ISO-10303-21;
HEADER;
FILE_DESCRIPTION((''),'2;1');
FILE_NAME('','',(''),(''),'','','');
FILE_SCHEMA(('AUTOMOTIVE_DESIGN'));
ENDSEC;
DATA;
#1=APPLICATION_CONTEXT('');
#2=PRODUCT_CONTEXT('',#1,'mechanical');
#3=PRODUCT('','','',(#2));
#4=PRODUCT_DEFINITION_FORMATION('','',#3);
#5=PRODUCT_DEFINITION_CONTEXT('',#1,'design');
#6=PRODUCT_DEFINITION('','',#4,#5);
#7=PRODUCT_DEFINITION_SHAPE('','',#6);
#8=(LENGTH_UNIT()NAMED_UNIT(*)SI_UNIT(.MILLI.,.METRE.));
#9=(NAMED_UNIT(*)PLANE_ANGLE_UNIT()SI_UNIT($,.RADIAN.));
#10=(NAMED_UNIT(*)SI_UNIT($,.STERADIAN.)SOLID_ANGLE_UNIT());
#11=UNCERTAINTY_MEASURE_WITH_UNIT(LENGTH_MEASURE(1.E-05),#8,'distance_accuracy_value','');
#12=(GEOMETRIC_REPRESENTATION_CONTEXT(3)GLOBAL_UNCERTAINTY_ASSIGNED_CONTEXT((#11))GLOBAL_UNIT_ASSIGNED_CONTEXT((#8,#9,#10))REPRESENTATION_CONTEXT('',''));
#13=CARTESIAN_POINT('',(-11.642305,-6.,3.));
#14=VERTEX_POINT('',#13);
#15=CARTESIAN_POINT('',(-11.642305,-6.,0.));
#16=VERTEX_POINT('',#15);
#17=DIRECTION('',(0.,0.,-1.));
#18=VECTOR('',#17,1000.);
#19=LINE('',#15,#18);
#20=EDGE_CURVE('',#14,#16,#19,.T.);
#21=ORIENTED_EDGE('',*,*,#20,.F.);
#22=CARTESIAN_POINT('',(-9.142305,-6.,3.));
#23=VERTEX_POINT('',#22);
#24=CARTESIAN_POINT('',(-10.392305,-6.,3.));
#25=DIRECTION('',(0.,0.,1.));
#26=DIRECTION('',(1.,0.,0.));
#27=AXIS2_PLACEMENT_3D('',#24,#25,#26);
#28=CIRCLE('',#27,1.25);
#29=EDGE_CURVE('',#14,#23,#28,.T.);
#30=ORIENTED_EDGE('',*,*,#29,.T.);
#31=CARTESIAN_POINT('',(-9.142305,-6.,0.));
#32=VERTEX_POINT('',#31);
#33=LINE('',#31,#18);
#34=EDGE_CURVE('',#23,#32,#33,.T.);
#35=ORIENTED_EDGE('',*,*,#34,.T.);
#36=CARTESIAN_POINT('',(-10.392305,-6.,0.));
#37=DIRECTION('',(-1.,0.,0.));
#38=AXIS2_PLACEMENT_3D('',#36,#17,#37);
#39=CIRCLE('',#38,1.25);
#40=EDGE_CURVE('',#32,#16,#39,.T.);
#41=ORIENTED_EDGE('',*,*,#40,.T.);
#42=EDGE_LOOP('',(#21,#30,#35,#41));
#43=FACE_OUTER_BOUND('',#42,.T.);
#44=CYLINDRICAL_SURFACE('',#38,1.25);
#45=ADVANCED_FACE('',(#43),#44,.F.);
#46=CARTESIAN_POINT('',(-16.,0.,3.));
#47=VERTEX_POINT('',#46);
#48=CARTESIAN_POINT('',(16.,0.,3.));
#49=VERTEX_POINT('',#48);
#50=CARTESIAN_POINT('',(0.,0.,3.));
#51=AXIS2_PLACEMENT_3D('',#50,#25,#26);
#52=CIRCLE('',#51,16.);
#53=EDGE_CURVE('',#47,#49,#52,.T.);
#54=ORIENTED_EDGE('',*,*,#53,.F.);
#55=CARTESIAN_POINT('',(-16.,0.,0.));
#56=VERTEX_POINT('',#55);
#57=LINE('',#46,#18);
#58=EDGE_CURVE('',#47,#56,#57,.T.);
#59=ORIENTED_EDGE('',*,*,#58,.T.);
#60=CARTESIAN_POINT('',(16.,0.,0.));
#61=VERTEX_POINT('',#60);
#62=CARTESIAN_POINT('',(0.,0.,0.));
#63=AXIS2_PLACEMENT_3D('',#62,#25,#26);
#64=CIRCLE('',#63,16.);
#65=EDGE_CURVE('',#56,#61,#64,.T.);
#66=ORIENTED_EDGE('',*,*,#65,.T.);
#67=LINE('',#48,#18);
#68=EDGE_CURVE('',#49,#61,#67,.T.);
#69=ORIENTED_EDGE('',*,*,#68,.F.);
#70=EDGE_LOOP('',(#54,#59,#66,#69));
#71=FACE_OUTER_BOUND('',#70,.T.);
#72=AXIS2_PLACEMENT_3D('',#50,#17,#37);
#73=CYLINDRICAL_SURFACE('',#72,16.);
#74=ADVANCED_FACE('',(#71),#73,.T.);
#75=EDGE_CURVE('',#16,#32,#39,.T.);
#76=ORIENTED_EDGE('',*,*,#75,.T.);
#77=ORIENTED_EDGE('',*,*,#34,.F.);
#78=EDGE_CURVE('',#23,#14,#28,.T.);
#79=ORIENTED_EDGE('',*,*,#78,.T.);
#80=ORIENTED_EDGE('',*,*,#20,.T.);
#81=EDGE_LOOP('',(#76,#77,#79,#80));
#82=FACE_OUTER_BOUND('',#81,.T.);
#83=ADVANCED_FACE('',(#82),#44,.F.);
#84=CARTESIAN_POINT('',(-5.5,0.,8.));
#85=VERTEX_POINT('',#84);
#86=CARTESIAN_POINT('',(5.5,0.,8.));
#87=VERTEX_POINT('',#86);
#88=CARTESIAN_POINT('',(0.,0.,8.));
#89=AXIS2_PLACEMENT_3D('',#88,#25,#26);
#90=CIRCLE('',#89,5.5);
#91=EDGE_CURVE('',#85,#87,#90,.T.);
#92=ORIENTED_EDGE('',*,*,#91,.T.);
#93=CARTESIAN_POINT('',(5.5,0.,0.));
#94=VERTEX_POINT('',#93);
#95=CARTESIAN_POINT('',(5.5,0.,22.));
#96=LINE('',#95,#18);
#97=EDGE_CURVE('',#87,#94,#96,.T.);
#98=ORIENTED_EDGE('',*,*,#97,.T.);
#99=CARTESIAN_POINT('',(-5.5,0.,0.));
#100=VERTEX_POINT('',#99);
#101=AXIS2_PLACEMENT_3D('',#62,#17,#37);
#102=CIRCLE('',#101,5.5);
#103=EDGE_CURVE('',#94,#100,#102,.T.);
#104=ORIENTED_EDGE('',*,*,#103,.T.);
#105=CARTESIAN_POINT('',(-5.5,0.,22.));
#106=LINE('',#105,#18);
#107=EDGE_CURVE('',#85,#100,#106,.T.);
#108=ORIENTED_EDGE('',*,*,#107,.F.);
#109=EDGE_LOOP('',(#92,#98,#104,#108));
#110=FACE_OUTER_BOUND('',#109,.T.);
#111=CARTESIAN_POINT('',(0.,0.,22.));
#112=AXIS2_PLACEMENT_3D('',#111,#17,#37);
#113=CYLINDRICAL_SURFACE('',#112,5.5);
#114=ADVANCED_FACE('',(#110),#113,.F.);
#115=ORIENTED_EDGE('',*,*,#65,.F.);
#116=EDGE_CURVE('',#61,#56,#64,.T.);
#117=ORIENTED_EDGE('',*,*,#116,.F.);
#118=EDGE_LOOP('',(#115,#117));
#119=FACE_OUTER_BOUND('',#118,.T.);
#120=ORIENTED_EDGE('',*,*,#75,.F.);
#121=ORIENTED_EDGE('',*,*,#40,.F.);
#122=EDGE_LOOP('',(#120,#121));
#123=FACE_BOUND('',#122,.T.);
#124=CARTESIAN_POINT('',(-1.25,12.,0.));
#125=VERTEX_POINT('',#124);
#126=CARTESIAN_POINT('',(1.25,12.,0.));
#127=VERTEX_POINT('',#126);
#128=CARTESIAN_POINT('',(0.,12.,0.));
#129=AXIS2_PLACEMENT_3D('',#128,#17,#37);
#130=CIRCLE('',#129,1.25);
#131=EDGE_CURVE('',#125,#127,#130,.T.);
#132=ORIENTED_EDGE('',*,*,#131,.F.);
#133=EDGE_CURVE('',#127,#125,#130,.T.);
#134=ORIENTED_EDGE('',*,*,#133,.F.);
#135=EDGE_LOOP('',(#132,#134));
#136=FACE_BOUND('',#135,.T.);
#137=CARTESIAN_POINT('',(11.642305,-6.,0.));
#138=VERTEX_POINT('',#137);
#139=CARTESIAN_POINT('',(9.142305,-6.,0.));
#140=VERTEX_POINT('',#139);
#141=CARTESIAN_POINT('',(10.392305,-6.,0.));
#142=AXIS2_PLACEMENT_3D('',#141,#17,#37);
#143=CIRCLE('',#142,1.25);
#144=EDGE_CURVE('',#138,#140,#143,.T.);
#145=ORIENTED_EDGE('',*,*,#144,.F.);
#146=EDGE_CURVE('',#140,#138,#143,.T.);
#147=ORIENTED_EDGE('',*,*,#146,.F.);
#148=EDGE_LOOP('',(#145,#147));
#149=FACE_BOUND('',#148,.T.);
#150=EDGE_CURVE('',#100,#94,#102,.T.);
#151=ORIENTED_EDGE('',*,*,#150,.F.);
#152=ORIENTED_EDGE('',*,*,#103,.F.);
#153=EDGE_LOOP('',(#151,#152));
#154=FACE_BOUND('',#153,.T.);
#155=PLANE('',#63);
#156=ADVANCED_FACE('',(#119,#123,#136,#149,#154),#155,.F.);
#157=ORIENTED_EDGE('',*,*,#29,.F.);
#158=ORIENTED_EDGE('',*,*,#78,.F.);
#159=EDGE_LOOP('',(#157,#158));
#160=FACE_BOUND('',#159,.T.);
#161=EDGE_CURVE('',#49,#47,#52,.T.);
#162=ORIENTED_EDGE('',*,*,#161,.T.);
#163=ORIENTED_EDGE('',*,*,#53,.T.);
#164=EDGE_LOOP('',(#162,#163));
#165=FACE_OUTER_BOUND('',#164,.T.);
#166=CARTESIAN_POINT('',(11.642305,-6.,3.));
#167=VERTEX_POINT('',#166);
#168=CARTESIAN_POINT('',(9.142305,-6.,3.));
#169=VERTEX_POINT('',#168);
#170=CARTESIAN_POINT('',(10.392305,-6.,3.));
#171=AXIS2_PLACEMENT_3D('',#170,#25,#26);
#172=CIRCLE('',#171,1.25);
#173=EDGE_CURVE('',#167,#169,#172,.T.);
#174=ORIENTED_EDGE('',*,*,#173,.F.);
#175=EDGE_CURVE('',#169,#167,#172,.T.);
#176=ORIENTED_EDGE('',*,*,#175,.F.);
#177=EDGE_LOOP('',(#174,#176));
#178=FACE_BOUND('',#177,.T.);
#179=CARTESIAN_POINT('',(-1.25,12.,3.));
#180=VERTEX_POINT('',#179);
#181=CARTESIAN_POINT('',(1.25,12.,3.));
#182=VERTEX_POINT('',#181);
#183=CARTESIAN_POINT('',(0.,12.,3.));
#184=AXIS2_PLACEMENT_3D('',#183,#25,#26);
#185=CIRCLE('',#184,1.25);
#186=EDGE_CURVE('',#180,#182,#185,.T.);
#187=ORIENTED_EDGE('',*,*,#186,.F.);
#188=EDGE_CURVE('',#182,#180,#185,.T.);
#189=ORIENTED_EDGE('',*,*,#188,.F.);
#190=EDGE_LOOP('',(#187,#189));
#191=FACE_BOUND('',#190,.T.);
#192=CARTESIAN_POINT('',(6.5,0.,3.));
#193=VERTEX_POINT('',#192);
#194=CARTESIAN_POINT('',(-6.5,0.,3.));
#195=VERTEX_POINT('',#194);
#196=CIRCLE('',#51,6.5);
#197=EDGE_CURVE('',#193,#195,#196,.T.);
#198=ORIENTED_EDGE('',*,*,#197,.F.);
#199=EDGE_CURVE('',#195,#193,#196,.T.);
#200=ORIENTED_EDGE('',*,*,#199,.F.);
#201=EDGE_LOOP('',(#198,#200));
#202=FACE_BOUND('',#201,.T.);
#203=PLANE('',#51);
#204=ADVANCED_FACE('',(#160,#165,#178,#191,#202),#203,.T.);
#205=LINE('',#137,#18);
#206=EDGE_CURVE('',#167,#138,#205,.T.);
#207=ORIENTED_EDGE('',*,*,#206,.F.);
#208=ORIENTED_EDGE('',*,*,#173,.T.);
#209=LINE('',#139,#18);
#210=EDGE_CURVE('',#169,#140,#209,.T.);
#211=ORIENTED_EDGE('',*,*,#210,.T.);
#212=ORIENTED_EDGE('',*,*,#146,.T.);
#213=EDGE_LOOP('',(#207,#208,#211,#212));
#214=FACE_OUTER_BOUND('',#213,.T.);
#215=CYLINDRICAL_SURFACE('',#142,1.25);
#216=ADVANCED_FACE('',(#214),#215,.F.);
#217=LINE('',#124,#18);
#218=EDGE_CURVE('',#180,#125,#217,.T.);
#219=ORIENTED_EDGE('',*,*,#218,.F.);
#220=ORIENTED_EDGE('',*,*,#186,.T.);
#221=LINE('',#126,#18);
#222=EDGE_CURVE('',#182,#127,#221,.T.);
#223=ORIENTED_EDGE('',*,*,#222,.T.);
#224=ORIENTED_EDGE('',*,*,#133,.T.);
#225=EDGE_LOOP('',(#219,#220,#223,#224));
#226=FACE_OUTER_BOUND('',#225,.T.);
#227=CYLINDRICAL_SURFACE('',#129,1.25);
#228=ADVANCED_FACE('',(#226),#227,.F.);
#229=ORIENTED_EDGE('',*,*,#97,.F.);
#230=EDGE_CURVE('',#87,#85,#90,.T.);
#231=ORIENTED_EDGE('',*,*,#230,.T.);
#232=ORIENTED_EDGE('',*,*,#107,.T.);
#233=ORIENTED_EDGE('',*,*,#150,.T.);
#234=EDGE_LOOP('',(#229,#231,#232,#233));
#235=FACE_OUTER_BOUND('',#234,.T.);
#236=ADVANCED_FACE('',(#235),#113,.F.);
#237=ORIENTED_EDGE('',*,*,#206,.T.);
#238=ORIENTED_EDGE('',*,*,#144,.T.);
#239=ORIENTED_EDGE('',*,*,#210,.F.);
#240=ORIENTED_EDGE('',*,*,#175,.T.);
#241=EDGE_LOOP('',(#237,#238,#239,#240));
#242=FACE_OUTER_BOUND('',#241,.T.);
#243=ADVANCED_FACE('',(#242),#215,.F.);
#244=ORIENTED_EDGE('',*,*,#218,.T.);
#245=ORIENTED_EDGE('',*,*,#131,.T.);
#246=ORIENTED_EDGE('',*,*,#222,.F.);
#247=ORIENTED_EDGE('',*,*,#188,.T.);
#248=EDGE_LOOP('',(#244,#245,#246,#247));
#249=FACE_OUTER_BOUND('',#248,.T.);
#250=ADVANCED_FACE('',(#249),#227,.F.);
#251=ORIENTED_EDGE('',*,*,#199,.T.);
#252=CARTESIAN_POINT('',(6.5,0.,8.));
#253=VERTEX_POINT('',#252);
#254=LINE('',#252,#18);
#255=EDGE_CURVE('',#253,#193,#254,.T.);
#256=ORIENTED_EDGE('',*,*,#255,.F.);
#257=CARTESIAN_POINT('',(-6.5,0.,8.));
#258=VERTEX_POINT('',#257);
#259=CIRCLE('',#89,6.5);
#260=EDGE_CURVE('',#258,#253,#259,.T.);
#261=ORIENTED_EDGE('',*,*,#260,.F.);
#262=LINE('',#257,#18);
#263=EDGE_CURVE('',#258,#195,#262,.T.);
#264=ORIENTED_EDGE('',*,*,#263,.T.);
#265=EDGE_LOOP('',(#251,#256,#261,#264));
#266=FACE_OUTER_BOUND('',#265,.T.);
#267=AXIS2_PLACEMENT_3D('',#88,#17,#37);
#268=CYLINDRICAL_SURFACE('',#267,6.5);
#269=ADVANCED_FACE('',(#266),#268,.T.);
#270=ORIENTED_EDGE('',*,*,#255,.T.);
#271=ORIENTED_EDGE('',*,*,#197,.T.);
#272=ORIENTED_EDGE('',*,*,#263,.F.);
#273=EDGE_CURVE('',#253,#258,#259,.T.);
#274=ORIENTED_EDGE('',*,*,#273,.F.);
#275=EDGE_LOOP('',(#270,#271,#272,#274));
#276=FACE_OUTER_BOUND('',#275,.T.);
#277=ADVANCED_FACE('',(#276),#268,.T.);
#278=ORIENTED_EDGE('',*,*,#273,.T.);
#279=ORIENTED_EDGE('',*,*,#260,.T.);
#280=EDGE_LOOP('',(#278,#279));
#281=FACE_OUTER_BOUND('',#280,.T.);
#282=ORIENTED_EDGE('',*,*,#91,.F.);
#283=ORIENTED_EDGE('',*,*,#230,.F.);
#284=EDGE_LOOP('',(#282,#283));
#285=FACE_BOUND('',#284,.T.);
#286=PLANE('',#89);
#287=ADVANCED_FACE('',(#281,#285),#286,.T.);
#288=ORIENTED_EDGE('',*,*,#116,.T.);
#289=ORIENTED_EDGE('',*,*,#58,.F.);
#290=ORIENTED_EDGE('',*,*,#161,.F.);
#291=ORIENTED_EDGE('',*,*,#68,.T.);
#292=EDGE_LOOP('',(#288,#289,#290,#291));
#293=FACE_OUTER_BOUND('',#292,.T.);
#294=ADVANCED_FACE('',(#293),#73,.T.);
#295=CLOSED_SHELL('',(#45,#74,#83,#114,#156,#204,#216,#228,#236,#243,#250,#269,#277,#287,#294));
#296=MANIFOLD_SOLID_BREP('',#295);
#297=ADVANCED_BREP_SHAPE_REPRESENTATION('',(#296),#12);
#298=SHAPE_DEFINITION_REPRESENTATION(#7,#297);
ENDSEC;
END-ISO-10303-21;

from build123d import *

# Parameters (mm, degrees)
SKETCH1_R             = 16
BOSS_EXTRUDE1_DEPTH   = 3
SKETCH2_R             = 6.5
BOSS_EXTRUDE2_DEPTH   = 5
SKETCH3_R             = 5.5
CUT_EXTRUDE1_DEPTH    = 22
SKETCH4_R             = 1
CUT_EXTRUDE2_DEPTH    = 10
M3_TAPPED_HOLE1_D     = 2.5
M3_TAPPED_HOLE1_DEPTH = 8


with BuildPart() as part:
    # Sketch1 → Boss-Extrude1 (new body)
    with BuildSketch(Plane.XY):
        Circle(SKETCH1_R)
    extrude(amount=BOSS_EXTRUDE1_DEPTH)

    # Sketch2 → Boss-Extrude2 (add)
    with BuildSketch(Plane.XY.offset(3)):
        Circle(SKETCH2_R)
    extrude(amount=BOSS_EXTRUDE2_DEPTH)

    # Sketch3 → Cut-Extrude1 (cut)
    with BuildSketch(Plane(origin=(0, 0, 0), x_dir=(-1, 0, 0), z_dir=(0, 0, -1))):
        Circle(SKETCH3_R)
    extrude(amount=-CUT_EXTRUDE1_DEPTH, mode=Mode.SUBTRACT)

    # Sketch4 → Cut-Extrude2 (cut)
    with BuildSketch(Plane(origin=(0, 0, 0), x_dir=(-1, 0, 0), z_dir=(0, 0, -1))):
        with Locations((0, 12)):
            Circle(SKETCH4_R)
        with Locations((10.392304845, -6)):
            Circle(SKETCH4_R)
        with Locations((-10.392304845, -6)):
            Circle(SKETCH4_R)
    extrude(amount=-CUT_EXTRUDE2_DEPTH, mode=Mode.SUBTRACT)

    # M3 Tapped Hole1
    with Locations(Plane(origin=(0, 0, 0), x_dir=(-1, 0, 0), z_dir=(0, 0, -1))):
        with Locations((0, 12), (10.392304845, -6), (-10.392304845, -6)):
            Hole(M3_TAPPED_HOLE1_D / 2, depth=M3_TAPPED_HOLE1_DEPTH)


solid = part.part
